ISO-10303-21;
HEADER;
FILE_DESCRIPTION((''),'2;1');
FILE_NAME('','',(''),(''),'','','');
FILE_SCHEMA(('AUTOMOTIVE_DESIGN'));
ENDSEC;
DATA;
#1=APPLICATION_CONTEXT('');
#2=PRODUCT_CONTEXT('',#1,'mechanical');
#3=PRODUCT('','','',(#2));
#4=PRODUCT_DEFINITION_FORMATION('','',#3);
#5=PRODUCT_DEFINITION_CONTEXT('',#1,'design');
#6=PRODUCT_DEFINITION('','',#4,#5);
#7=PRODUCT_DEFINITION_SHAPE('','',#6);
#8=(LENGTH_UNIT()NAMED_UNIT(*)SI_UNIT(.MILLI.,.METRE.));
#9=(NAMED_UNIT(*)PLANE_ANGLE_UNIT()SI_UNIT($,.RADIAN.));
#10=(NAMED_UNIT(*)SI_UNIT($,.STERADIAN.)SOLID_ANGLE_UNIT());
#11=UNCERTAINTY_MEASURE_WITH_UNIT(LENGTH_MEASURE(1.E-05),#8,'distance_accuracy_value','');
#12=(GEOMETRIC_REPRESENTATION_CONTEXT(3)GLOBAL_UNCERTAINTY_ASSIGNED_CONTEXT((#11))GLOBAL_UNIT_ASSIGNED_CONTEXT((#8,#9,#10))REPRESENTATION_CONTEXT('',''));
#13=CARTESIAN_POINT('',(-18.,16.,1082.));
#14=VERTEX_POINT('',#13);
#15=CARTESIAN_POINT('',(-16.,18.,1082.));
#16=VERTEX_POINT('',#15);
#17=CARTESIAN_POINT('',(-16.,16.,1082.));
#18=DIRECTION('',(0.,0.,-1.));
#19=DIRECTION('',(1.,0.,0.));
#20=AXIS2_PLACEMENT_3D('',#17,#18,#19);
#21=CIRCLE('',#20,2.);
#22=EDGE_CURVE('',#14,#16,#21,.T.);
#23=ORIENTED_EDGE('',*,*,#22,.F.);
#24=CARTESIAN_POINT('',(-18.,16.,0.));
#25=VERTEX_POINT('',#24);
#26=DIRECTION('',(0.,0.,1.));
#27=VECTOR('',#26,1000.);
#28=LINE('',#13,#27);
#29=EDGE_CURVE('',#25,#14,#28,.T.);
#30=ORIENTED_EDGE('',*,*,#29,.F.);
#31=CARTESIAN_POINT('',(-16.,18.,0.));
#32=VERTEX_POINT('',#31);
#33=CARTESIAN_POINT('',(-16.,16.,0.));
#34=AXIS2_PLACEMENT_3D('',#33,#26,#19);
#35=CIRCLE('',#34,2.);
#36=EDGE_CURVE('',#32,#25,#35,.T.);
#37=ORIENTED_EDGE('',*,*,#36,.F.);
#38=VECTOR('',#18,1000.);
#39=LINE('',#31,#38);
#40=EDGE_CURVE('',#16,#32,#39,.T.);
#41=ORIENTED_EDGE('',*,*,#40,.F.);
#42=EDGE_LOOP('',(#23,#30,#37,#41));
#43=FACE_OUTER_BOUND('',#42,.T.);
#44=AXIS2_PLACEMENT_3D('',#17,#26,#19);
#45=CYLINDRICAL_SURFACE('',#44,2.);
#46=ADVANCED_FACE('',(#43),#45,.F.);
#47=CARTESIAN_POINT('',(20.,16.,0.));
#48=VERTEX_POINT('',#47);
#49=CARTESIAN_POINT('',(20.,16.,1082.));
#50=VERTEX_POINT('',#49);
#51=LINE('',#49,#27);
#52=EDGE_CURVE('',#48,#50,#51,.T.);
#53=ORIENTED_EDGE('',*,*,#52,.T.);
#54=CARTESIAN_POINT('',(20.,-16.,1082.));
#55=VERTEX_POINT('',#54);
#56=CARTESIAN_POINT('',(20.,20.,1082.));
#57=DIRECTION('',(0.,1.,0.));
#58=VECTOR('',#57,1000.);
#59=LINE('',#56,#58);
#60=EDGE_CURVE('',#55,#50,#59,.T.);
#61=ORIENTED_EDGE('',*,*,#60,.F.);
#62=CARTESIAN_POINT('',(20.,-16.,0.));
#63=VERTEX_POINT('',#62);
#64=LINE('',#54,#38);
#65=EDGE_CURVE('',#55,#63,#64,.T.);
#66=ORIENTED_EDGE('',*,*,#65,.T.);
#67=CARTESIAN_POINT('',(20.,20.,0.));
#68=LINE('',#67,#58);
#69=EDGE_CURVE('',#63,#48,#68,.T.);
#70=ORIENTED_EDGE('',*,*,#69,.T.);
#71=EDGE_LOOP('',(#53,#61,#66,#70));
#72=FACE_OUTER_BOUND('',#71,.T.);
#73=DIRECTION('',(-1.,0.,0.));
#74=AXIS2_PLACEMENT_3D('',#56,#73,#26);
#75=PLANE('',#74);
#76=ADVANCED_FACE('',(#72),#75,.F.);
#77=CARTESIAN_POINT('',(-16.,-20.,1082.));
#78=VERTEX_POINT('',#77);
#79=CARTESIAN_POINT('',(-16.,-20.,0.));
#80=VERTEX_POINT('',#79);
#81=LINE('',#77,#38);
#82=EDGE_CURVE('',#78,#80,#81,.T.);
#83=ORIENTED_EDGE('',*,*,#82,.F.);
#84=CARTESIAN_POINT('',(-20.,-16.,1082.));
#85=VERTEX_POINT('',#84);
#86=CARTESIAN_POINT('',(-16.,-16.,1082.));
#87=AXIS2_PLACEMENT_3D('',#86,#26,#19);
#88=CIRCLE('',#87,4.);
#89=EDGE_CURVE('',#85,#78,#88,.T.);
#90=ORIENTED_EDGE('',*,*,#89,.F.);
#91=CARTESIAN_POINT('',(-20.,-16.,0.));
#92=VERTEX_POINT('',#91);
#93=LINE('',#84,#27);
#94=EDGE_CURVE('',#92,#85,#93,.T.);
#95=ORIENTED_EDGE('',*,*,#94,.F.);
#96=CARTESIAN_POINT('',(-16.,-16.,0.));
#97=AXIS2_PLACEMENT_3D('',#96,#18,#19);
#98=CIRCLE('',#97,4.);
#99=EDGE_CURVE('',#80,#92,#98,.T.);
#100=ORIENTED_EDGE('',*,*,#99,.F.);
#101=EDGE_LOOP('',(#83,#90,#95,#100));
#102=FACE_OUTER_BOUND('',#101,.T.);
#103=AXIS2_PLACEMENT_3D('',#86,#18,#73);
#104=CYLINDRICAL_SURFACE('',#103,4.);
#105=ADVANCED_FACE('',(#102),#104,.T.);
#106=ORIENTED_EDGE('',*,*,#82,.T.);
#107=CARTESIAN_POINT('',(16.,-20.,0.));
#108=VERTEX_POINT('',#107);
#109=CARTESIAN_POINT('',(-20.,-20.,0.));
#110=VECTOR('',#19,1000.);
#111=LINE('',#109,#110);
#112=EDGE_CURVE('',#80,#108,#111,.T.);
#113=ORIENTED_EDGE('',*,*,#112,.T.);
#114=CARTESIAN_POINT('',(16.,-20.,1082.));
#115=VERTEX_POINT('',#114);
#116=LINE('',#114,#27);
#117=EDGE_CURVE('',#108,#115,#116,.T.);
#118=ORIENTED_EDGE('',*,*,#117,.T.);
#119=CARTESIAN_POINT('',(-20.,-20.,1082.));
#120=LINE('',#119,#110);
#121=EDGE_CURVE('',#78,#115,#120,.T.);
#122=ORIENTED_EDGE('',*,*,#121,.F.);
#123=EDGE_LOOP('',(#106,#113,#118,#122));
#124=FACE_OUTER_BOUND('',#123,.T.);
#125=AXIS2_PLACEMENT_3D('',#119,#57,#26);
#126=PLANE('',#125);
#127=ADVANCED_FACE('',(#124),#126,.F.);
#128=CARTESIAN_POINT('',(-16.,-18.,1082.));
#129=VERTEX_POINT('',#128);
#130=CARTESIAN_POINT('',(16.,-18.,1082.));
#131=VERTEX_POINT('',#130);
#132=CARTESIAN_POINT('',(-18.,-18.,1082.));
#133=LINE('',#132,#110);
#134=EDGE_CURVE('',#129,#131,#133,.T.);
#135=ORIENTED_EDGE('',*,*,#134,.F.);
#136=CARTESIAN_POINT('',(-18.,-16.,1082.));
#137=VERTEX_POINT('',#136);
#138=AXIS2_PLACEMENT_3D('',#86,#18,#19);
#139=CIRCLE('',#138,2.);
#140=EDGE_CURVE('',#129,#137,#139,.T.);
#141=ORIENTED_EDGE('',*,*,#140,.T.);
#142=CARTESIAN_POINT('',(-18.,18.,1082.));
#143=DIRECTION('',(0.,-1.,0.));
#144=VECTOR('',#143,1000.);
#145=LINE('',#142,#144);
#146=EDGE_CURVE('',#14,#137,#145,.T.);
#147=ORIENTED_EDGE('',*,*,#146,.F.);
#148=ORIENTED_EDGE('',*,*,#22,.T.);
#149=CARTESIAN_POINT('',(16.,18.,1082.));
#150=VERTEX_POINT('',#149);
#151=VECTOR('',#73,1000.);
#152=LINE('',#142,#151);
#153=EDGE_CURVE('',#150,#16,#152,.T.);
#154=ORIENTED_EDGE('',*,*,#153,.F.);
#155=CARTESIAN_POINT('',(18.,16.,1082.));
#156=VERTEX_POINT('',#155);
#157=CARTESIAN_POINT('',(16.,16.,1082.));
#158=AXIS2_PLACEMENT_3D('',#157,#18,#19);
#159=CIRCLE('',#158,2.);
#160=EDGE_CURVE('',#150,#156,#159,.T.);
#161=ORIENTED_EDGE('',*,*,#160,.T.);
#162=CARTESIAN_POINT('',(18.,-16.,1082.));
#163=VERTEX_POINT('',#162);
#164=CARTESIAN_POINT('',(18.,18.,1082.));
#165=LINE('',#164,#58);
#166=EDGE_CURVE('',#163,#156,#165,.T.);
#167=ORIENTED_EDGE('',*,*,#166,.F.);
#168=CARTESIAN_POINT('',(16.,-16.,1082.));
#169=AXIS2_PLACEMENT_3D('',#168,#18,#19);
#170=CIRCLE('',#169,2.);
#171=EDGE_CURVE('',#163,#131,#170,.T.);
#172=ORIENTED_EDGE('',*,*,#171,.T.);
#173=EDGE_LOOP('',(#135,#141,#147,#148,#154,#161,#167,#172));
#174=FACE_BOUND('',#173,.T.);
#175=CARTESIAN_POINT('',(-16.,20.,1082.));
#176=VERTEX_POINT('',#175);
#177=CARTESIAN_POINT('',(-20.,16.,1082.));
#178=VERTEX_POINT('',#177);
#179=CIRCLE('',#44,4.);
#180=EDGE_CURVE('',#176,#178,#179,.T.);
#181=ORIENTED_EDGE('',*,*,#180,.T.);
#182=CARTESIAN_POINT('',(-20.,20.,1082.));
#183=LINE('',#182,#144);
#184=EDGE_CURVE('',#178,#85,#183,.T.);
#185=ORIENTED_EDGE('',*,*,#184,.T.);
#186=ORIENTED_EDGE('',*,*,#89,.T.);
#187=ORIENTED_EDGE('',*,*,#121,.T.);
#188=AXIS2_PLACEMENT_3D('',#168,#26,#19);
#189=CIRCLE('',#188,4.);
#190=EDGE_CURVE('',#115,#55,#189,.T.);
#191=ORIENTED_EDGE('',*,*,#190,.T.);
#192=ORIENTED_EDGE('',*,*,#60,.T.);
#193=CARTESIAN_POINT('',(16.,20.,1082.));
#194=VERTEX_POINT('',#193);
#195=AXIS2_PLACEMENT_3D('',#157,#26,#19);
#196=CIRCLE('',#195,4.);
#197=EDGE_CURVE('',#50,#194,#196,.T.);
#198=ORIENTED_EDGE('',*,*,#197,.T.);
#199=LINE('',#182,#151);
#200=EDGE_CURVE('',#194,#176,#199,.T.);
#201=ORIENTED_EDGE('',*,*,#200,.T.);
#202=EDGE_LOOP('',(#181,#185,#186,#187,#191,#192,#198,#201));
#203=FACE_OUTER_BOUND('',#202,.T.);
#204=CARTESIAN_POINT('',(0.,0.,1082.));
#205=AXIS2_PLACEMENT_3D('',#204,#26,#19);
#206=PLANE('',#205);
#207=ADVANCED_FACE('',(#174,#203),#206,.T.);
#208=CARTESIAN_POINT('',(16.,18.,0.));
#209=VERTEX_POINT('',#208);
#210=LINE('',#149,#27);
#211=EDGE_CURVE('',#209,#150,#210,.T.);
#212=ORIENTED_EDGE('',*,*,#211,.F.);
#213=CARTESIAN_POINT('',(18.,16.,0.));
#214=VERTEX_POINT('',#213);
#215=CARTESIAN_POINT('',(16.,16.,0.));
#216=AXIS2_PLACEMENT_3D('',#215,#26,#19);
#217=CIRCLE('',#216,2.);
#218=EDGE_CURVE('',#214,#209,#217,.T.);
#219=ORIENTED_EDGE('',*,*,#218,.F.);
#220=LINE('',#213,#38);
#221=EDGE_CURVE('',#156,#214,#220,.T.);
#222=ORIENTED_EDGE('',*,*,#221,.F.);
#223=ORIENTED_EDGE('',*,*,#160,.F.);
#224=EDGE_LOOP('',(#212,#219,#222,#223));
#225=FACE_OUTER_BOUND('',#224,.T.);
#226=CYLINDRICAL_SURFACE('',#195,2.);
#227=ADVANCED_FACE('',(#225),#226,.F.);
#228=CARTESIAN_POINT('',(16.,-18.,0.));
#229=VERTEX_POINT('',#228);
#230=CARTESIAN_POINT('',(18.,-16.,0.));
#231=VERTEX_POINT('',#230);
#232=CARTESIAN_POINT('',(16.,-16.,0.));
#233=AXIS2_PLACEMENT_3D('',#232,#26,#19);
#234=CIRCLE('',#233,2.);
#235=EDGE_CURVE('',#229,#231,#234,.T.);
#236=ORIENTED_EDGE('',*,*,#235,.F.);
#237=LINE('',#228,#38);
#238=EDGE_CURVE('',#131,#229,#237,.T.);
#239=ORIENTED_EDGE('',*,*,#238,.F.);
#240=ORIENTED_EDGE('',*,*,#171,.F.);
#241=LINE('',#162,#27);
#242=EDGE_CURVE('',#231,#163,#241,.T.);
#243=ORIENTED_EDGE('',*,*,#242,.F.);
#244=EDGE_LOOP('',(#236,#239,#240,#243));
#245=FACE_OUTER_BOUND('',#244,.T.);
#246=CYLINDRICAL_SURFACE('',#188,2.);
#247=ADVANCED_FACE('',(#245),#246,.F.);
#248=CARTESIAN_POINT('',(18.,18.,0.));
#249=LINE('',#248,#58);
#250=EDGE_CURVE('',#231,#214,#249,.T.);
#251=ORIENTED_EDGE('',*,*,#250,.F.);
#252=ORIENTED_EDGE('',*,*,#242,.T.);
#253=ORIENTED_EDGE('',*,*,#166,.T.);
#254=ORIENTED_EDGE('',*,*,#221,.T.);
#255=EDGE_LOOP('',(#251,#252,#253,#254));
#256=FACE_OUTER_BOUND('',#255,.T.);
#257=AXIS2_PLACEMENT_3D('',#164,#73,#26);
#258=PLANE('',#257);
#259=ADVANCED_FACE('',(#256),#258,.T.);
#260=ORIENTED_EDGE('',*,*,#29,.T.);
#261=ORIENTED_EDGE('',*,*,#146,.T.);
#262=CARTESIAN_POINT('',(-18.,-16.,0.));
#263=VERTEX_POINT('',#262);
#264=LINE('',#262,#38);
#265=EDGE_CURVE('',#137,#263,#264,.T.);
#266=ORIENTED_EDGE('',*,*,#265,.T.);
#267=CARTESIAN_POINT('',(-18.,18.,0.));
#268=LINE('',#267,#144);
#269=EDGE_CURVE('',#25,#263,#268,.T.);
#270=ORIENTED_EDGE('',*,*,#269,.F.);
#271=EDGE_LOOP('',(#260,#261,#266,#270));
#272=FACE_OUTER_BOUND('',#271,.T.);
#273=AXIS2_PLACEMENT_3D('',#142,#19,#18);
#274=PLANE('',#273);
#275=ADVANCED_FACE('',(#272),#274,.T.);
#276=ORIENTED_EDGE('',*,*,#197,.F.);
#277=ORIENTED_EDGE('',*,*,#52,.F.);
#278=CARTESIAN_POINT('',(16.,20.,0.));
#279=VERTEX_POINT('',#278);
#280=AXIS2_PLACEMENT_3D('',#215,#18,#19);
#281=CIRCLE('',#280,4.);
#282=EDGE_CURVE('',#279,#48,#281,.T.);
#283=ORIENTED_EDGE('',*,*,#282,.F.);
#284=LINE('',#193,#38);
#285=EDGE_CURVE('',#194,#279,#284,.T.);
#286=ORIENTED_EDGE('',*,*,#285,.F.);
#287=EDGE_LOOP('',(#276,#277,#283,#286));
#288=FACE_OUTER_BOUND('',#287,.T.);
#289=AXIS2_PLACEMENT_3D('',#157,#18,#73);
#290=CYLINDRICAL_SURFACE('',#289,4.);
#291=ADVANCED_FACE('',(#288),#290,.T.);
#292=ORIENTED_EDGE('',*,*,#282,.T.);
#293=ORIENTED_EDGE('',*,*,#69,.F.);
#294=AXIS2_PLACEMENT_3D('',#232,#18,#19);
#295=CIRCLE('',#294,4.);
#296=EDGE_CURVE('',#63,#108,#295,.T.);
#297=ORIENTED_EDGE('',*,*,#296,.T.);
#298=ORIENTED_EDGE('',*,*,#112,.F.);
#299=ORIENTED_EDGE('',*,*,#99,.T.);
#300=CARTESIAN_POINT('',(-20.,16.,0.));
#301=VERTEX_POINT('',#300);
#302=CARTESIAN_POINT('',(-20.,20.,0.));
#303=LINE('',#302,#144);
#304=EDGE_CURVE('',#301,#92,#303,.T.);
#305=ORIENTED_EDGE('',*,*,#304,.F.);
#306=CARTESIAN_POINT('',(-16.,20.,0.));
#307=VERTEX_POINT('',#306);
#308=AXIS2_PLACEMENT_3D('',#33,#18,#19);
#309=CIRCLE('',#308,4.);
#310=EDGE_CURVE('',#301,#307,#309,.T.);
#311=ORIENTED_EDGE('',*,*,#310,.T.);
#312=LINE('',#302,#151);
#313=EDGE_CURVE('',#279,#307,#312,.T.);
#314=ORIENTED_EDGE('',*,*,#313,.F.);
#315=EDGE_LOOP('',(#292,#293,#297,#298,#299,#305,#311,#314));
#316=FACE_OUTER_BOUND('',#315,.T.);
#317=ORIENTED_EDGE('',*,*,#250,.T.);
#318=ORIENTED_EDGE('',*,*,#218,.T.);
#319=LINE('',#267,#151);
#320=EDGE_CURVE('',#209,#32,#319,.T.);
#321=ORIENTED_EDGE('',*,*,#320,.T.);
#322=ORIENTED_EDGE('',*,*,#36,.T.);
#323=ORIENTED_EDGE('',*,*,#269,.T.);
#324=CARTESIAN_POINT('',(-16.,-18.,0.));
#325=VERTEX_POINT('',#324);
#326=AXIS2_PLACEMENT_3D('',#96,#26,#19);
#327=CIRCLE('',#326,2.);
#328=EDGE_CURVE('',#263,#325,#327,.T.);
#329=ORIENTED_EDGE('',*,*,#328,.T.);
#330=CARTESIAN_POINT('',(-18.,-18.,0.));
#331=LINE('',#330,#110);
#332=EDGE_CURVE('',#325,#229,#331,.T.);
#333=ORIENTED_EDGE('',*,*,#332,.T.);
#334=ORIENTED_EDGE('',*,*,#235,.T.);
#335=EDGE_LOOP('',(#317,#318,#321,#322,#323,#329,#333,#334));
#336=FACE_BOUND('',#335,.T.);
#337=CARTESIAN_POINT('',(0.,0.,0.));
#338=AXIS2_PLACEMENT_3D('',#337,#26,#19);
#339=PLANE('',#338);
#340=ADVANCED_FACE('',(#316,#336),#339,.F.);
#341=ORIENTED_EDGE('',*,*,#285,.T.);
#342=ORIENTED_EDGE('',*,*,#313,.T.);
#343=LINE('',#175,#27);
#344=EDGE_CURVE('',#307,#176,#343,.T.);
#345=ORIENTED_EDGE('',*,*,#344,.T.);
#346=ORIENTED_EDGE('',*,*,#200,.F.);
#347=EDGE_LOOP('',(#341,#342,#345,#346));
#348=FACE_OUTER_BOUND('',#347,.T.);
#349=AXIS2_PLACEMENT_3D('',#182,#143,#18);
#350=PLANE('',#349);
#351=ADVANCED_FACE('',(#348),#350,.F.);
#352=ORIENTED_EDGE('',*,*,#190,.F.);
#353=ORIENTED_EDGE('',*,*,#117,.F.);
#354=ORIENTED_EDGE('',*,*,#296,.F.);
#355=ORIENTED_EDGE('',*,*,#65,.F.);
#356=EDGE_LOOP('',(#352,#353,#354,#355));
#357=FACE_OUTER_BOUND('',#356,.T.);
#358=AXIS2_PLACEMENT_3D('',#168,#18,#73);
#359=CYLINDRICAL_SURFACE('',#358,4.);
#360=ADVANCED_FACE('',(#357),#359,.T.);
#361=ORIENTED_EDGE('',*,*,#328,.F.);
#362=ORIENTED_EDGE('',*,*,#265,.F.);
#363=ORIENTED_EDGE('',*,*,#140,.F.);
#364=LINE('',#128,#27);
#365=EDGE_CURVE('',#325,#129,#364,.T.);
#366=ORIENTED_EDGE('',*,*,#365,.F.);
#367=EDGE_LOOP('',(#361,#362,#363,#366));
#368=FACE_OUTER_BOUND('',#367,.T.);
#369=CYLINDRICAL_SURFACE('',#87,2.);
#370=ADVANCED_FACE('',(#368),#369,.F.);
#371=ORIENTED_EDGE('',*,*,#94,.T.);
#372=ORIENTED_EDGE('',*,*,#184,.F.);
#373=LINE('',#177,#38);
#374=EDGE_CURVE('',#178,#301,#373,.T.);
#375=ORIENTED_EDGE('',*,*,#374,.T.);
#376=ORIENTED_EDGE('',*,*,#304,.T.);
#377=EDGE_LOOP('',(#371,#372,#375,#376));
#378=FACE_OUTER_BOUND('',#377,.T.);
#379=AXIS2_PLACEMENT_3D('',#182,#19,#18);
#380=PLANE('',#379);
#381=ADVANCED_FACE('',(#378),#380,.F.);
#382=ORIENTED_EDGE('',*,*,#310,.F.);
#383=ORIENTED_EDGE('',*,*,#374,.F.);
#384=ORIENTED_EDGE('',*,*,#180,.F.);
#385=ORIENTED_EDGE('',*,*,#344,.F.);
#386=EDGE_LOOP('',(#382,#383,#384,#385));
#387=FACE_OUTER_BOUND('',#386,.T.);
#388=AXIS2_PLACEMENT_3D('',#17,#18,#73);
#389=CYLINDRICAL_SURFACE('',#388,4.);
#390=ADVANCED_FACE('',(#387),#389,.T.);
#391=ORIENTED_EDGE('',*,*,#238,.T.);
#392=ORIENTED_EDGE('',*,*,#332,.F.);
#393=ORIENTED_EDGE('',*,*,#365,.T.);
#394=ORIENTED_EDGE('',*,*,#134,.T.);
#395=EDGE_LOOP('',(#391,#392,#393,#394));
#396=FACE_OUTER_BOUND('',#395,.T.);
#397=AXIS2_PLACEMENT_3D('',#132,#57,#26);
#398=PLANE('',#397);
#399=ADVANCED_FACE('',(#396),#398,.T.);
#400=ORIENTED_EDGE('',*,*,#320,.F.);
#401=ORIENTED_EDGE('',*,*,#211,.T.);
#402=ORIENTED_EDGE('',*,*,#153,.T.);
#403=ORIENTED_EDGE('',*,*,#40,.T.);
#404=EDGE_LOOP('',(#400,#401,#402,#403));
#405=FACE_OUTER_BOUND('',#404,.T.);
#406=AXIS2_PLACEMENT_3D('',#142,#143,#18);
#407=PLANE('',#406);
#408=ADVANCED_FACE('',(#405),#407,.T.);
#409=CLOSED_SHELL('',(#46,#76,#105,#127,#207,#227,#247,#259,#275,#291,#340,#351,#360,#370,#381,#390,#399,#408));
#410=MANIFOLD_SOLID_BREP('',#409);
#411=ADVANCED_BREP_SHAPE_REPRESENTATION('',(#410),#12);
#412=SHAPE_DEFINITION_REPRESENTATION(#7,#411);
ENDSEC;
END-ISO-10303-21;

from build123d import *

# Parameters (mm, degrees)
SKETCH1_W           = 40
SKETCH1_H           = 40
SKETCH1_W_2         = 36
SKETCH1_H_2         = 36
BOSS_EXTRUDE1_DEPTH = 1082
FILLET1_R           = 2
FILLET2_R           = 4


with BuildPart() as part:
    # Sketch1 → Boss-Extrude1 (new body)
    with BuildSketch(Plane.XY):
        Rectangle(SKETCH1_W, SKETCH1_H)
        Rectangle(SKETCH1_W_2, SKETCH1_H_2, mode=Mode.SUBTRACT)
    extrude(amount=BOSS_EXTRUDE1_DEPTH)

    # Fillet1
    fillet1_edges = [part.edges().sort_by_distance(p)[0] for p in [
        (18, -18, 541),
        (18, 18, 541),
        (-18, 18, 541),
        (-18, -18, 541),
    ]]
    fillet(fillet1_edges, radius=FILLET1_R)

    # Fillet2
    fillet2_edges = [part.edges().sort_by_distance(p)[0] for p in [
        (20, -20, 541),
        (-20, -20, 541),
        (-20, 20, 541),
        (20, 20, 541),
    ]]
    fillet(fillet2_edges, radius=FILLET2_R)


solid = part.part
